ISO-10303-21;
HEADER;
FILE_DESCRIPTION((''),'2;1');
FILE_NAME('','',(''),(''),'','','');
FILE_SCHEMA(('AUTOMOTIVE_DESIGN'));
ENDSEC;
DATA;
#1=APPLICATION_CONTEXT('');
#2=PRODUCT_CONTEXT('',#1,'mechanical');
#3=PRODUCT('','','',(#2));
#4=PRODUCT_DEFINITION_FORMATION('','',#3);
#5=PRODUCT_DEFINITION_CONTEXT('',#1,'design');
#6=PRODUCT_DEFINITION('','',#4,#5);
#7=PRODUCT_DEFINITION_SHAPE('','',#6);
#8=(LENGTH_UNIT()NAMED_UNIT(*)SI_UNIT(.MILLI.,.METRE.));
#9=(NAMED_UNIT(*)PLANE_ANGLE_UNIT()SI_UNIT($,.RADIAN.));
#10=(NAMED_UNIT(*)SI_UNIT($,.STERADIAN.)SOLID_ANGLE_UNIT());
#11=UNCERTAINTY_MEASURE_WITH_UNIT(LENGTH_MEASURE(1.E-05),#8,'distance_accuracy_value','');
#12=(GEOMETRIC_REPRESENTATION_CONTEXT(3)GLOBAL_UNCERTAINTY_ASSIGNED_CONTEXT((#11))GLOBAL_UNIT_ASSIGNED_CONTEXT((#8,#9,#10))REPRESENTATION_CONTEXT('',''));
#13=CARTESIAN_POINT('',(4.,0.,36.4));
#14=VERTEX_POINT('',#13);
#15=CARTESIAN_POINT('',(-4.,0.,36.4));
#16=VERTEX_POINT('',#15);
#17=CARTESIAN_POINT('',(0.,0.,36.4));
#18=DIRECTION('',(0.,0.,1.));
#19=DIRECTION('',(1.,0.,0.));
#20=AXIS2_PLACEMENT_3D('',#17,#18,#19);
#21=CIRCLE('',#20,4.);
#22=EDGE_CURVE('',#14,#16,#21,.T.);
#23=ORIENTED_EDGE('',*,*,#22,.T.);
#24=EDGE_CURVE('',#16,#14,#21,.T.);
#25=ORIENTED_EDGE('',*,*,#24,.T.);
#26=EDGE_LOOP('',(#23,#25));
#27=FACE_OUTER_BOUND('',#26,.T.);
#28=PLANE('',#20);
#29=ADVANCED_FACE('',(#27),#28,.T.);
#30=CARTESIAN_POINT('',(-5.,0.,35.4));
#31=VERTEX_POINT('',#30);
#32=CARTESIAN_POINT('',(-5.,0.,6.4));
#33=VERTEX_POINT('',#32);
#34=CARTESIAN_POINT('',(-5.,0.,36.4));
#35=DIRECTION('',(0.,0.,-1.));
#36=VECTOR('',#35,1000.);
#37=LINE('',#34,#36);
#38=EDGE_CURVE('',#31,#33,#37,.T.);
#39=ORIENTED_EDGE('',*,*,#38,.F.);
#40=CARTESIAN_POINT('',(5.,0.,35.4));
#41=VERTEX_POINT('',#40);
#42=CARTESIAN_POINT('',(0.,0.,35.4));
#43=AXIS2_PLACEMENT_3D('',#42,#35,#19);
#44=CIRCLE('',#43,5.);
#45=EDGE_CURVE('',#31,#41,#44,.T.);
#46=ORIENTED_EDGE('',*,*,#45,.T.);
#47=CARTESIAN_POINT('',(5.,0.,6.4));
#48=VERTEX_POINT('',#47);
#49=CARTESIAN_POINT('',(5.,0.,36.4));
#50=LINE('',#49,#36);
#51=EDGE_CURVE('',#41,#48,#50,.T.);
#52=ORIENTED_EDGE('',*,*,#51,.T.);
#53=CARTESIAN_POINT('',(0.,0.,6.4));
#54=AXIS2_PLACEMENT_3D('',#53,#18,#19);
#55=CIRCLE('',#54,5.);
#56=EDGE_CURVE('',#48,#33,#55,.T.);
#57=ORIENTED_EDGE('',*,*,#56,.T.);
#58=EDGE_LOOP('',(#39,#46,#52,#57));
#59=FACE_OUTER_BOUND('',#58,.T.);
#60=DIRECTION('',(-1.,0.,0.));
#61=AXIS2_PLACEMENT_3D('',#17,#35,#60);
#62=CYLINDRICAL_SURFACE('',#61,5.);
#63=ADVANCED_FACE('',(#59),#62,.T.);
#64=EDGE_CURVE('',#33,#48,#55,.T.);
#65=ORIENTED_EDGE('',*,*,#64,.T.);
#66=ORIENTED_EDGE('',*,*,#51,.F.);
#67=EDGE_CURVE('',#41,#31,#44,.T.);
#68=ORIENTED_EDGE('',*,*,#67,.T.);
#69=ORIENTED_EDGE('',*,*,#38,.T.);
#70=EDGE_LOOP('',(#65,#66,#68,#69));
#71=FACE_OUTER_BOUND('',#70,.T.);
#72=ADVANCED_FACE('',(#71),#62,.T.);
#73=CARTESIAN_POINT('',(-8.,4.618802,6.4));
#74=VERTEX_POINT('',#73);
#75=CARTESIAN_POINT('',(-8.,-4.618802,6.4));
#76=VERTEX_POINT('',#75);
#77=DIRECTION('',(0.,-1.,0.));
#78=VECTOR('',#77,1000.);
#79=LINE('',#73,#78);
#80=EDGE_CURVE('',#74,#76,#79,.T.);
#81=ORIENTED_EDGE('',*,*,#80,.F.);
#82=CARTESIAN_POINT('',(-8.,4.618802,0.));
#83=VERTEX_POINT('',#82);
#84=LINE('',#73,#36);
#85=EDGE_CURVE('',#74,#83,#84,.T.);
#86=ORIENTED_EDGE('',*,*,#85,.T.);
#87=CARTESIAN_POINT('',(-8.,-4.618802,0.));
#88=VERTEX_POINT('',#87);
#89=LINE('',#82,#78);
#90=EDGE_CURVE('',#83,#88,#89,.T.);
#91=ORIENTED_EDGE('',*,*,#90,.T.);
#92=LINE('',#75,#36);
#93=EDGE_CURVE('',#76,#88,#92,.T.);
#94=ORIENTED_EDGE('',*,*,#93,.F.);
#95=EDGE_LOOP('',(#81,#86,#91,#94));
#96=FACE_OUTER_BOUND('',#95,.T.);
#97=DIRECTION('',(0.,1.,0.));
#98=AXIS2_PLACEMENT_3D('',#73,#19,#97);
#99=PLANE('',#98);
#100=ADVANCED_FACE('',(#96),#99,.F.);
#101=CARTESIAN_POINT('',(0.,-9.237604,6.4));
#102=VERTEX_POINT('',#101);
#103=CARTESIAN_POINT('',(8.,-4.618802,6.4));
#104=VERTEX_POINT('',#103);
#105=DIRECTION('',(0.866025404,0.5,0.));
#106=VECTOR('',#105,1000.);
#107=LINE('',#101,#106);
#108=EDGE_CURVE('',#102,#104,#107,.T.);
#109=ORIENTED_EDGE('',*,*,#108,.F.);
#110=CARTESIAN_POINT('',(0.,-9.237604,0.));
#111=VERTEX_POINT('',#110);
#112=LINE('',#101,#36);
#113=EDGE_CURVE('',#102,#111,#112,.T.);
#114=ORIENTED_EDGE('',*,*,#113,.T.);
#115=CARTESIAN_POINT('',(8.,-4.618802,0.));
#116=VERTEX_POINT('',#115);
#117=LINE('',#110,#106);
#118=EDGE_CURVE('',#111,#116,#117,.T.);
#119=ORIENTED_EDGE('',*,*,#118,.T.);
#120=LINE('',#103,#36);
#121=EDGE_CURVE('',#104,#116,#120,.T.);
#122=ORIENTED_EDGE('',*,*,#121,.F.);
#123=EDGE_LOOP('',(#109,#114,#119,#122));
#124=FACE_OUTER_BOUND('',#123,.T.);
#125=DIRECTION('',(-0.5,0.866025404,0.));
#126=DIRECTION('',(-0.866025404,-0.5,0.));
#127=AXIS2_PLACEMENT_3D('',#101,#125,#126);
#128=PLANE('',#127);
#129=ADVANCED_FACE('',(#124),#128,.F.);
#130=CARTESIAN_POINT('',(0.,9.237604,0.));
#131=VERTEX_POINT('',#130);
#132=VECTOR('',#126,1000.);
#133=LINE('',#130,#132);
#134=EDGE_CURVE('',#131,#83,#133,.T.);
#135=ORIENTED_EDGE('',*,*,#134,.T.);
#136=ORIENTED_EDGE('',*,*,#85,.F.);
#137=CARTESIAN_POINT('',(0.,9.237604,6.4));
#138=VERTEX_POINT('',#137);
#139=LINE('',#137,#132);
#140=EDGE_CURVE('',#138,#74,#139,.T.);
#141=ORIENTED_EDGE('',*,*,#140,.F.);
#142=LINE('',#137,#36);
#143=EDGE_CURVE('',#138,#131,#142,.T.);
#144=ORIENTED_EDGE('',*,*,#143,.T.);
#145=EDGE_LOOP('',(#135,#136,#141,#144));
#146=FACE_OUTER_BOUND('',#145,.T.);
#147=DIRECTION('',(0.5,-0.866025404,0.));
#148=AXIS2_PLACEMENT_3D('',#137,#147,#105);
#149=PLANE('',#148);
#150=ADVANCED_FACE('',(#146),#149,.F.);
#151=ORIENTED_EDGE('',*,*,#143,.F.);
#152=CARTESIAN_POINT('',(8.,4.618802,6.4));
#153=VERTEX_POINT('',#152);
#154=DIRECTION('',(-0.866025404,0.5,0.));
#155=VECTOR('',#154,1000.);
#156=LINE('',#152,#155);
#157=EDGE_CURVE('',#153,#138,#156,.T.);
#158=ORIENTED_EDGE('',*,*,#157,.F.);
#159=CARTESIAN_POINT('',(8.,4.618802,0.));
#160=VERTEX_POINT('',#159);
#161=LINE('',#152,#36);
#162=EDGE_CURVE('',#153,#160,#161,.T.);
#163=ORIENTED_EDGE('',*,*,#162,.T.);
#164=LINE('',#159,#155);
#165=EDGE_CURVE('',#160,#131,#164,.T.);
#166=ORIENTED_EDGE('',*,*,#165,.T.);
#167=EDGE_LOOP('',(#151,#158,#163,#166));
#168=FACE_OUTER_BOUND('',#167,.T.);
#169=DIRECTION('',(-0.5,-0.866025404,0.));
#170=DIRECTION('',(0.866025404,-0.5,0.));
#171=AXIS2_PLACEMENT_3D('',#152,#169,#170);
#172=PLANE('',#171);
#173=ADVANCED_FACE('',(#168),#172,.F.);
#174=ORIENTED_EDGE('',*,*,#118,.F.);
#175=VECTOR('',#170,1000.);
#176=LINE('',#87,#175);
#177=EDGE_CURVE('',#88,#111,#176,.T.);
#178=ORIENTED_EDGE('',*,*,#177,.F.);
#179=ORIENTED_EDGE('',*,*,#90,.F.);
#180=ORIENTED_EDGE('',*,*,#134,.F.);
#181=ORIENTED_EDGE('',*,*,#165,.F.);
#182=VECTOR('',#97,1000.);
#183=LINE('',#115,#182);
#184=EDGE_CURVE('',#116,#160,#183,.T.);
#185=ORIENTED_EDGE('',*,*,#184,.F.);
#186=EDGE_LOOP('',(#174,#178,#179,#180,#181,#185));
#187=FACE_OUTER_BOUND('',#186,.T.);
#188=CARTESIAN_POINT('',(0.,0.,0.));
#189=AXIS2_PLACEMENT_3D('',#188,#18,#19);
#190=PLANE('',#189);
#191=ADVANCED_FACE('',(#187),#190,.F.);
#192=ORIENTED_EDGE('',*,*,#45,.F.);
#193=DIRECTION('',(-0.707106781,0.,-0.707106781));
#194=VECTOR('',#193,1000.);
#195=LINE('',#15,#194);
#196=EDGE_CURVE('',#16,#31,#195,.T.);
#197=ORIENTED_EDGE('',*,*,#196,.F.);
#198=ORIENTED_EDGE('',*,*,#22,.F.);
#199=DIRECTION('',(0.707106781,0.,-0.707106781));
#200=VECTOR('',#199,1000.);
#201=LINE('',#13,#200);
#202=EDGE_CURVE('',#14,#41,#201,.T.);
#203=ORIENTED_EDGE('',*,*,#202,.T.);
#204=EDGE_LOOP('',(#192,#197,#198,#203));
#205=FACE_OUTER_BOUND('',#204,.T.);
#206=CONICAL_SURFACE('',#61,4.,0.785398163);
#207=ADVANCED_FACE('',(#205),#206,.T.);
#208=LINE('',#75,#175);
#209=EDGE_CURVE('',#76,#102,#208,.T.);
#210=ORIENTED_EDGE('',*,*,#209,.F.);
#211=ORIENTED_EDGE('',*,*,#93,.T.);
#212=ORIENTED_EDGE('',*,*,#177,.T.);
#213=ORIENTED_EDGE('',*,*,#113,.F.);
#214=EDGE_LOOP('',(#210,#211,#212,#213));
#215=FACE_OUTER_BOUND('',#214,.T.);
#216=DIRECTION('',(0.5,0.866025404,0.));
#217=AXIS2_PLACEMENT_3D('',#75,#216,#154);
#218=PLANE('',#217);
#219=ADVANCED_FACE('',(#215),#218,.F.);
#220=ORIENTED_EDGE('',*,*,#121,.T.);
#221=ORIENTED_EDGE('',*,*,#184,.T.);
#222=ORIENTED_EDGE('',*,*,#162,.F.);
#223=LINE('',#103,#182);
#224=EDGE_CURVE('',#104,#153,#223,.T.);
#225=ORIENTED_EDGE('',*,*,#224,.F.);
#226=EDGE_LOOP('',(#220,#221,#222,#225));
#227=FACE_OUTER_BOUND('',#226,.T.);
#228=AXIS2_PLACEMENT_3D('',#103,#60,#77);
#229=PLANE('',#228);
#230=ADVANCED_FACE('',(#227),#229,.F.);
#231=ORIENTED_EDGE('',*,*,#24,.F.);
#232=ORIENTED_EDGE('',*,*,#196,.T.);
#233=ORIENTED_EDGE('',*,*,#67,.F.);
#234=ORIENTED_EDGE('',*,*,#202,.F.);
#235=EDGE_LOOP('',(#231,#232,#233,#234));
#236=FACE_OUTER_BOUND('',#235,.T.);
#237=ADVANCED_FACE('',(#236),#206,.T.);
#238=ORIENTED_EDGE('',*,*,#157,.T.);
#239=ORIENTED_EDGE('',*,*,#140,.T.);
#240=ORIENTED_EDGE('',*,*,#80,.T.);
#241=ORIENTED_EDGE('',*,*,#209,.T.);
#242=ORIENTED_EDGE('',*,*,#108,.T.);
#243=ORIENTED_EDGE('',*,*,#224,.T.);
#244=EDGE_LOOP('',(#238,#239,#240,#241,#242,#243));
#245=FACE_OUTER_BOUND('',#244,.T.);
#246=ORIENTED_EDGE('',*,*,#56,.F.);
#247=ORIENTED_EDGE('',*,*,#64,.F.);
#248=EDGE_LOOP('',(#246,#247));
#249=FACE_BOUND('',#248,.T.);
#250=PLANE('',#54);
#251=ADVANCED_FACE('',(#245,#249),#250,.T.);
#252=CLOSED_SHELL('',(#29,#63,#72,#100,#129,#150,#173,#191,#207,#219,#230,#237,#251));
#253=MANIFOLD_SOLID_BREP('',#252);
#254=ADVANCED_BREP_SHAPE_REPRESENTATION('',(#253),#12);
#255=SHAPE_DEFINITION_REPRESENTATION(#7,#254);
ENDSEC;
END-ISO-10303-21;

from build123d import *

# Parameters (mm, degrees)
BOSS_EXTRUDE1_DEPTH = 6.4
SKETCH3_R           = 5
BOSS_EXTRUDE2_DEPTH = 30
CHAMFER1_SIZE       = 1


with BuildPart() as part:
    # Sketch1 → Boss-Extrude1 (new body)
    with BuildSketch(Plane.XY):
        Polygon((8, 4.618802154), (0, 9.237604307), (-8, 4.618802154), (-8, -4.618802154), (0, -9.237604307), (8, -4.618802154), align=None)
    extrude(amount=BOSS_EXTRUDE1_DEPTH)

    # Sketch3 → Boss-Extrude2 (add)
    with BuildSketch(Plane.XY.offset(6.4)):
        Circle(SKETCH3_R)
    extrude(amount=BOSS_EXTRUDE2_DEPTH)

    # Chamfer1
    chamfer1_edges = [part.edges().sort_by_distance(p)[0] for p in [
        (-5, 0, 36.4),
    ]]
    chamfer(chamfer1_edges, length=CHAMFER1_SIZE)


solid = part.part
